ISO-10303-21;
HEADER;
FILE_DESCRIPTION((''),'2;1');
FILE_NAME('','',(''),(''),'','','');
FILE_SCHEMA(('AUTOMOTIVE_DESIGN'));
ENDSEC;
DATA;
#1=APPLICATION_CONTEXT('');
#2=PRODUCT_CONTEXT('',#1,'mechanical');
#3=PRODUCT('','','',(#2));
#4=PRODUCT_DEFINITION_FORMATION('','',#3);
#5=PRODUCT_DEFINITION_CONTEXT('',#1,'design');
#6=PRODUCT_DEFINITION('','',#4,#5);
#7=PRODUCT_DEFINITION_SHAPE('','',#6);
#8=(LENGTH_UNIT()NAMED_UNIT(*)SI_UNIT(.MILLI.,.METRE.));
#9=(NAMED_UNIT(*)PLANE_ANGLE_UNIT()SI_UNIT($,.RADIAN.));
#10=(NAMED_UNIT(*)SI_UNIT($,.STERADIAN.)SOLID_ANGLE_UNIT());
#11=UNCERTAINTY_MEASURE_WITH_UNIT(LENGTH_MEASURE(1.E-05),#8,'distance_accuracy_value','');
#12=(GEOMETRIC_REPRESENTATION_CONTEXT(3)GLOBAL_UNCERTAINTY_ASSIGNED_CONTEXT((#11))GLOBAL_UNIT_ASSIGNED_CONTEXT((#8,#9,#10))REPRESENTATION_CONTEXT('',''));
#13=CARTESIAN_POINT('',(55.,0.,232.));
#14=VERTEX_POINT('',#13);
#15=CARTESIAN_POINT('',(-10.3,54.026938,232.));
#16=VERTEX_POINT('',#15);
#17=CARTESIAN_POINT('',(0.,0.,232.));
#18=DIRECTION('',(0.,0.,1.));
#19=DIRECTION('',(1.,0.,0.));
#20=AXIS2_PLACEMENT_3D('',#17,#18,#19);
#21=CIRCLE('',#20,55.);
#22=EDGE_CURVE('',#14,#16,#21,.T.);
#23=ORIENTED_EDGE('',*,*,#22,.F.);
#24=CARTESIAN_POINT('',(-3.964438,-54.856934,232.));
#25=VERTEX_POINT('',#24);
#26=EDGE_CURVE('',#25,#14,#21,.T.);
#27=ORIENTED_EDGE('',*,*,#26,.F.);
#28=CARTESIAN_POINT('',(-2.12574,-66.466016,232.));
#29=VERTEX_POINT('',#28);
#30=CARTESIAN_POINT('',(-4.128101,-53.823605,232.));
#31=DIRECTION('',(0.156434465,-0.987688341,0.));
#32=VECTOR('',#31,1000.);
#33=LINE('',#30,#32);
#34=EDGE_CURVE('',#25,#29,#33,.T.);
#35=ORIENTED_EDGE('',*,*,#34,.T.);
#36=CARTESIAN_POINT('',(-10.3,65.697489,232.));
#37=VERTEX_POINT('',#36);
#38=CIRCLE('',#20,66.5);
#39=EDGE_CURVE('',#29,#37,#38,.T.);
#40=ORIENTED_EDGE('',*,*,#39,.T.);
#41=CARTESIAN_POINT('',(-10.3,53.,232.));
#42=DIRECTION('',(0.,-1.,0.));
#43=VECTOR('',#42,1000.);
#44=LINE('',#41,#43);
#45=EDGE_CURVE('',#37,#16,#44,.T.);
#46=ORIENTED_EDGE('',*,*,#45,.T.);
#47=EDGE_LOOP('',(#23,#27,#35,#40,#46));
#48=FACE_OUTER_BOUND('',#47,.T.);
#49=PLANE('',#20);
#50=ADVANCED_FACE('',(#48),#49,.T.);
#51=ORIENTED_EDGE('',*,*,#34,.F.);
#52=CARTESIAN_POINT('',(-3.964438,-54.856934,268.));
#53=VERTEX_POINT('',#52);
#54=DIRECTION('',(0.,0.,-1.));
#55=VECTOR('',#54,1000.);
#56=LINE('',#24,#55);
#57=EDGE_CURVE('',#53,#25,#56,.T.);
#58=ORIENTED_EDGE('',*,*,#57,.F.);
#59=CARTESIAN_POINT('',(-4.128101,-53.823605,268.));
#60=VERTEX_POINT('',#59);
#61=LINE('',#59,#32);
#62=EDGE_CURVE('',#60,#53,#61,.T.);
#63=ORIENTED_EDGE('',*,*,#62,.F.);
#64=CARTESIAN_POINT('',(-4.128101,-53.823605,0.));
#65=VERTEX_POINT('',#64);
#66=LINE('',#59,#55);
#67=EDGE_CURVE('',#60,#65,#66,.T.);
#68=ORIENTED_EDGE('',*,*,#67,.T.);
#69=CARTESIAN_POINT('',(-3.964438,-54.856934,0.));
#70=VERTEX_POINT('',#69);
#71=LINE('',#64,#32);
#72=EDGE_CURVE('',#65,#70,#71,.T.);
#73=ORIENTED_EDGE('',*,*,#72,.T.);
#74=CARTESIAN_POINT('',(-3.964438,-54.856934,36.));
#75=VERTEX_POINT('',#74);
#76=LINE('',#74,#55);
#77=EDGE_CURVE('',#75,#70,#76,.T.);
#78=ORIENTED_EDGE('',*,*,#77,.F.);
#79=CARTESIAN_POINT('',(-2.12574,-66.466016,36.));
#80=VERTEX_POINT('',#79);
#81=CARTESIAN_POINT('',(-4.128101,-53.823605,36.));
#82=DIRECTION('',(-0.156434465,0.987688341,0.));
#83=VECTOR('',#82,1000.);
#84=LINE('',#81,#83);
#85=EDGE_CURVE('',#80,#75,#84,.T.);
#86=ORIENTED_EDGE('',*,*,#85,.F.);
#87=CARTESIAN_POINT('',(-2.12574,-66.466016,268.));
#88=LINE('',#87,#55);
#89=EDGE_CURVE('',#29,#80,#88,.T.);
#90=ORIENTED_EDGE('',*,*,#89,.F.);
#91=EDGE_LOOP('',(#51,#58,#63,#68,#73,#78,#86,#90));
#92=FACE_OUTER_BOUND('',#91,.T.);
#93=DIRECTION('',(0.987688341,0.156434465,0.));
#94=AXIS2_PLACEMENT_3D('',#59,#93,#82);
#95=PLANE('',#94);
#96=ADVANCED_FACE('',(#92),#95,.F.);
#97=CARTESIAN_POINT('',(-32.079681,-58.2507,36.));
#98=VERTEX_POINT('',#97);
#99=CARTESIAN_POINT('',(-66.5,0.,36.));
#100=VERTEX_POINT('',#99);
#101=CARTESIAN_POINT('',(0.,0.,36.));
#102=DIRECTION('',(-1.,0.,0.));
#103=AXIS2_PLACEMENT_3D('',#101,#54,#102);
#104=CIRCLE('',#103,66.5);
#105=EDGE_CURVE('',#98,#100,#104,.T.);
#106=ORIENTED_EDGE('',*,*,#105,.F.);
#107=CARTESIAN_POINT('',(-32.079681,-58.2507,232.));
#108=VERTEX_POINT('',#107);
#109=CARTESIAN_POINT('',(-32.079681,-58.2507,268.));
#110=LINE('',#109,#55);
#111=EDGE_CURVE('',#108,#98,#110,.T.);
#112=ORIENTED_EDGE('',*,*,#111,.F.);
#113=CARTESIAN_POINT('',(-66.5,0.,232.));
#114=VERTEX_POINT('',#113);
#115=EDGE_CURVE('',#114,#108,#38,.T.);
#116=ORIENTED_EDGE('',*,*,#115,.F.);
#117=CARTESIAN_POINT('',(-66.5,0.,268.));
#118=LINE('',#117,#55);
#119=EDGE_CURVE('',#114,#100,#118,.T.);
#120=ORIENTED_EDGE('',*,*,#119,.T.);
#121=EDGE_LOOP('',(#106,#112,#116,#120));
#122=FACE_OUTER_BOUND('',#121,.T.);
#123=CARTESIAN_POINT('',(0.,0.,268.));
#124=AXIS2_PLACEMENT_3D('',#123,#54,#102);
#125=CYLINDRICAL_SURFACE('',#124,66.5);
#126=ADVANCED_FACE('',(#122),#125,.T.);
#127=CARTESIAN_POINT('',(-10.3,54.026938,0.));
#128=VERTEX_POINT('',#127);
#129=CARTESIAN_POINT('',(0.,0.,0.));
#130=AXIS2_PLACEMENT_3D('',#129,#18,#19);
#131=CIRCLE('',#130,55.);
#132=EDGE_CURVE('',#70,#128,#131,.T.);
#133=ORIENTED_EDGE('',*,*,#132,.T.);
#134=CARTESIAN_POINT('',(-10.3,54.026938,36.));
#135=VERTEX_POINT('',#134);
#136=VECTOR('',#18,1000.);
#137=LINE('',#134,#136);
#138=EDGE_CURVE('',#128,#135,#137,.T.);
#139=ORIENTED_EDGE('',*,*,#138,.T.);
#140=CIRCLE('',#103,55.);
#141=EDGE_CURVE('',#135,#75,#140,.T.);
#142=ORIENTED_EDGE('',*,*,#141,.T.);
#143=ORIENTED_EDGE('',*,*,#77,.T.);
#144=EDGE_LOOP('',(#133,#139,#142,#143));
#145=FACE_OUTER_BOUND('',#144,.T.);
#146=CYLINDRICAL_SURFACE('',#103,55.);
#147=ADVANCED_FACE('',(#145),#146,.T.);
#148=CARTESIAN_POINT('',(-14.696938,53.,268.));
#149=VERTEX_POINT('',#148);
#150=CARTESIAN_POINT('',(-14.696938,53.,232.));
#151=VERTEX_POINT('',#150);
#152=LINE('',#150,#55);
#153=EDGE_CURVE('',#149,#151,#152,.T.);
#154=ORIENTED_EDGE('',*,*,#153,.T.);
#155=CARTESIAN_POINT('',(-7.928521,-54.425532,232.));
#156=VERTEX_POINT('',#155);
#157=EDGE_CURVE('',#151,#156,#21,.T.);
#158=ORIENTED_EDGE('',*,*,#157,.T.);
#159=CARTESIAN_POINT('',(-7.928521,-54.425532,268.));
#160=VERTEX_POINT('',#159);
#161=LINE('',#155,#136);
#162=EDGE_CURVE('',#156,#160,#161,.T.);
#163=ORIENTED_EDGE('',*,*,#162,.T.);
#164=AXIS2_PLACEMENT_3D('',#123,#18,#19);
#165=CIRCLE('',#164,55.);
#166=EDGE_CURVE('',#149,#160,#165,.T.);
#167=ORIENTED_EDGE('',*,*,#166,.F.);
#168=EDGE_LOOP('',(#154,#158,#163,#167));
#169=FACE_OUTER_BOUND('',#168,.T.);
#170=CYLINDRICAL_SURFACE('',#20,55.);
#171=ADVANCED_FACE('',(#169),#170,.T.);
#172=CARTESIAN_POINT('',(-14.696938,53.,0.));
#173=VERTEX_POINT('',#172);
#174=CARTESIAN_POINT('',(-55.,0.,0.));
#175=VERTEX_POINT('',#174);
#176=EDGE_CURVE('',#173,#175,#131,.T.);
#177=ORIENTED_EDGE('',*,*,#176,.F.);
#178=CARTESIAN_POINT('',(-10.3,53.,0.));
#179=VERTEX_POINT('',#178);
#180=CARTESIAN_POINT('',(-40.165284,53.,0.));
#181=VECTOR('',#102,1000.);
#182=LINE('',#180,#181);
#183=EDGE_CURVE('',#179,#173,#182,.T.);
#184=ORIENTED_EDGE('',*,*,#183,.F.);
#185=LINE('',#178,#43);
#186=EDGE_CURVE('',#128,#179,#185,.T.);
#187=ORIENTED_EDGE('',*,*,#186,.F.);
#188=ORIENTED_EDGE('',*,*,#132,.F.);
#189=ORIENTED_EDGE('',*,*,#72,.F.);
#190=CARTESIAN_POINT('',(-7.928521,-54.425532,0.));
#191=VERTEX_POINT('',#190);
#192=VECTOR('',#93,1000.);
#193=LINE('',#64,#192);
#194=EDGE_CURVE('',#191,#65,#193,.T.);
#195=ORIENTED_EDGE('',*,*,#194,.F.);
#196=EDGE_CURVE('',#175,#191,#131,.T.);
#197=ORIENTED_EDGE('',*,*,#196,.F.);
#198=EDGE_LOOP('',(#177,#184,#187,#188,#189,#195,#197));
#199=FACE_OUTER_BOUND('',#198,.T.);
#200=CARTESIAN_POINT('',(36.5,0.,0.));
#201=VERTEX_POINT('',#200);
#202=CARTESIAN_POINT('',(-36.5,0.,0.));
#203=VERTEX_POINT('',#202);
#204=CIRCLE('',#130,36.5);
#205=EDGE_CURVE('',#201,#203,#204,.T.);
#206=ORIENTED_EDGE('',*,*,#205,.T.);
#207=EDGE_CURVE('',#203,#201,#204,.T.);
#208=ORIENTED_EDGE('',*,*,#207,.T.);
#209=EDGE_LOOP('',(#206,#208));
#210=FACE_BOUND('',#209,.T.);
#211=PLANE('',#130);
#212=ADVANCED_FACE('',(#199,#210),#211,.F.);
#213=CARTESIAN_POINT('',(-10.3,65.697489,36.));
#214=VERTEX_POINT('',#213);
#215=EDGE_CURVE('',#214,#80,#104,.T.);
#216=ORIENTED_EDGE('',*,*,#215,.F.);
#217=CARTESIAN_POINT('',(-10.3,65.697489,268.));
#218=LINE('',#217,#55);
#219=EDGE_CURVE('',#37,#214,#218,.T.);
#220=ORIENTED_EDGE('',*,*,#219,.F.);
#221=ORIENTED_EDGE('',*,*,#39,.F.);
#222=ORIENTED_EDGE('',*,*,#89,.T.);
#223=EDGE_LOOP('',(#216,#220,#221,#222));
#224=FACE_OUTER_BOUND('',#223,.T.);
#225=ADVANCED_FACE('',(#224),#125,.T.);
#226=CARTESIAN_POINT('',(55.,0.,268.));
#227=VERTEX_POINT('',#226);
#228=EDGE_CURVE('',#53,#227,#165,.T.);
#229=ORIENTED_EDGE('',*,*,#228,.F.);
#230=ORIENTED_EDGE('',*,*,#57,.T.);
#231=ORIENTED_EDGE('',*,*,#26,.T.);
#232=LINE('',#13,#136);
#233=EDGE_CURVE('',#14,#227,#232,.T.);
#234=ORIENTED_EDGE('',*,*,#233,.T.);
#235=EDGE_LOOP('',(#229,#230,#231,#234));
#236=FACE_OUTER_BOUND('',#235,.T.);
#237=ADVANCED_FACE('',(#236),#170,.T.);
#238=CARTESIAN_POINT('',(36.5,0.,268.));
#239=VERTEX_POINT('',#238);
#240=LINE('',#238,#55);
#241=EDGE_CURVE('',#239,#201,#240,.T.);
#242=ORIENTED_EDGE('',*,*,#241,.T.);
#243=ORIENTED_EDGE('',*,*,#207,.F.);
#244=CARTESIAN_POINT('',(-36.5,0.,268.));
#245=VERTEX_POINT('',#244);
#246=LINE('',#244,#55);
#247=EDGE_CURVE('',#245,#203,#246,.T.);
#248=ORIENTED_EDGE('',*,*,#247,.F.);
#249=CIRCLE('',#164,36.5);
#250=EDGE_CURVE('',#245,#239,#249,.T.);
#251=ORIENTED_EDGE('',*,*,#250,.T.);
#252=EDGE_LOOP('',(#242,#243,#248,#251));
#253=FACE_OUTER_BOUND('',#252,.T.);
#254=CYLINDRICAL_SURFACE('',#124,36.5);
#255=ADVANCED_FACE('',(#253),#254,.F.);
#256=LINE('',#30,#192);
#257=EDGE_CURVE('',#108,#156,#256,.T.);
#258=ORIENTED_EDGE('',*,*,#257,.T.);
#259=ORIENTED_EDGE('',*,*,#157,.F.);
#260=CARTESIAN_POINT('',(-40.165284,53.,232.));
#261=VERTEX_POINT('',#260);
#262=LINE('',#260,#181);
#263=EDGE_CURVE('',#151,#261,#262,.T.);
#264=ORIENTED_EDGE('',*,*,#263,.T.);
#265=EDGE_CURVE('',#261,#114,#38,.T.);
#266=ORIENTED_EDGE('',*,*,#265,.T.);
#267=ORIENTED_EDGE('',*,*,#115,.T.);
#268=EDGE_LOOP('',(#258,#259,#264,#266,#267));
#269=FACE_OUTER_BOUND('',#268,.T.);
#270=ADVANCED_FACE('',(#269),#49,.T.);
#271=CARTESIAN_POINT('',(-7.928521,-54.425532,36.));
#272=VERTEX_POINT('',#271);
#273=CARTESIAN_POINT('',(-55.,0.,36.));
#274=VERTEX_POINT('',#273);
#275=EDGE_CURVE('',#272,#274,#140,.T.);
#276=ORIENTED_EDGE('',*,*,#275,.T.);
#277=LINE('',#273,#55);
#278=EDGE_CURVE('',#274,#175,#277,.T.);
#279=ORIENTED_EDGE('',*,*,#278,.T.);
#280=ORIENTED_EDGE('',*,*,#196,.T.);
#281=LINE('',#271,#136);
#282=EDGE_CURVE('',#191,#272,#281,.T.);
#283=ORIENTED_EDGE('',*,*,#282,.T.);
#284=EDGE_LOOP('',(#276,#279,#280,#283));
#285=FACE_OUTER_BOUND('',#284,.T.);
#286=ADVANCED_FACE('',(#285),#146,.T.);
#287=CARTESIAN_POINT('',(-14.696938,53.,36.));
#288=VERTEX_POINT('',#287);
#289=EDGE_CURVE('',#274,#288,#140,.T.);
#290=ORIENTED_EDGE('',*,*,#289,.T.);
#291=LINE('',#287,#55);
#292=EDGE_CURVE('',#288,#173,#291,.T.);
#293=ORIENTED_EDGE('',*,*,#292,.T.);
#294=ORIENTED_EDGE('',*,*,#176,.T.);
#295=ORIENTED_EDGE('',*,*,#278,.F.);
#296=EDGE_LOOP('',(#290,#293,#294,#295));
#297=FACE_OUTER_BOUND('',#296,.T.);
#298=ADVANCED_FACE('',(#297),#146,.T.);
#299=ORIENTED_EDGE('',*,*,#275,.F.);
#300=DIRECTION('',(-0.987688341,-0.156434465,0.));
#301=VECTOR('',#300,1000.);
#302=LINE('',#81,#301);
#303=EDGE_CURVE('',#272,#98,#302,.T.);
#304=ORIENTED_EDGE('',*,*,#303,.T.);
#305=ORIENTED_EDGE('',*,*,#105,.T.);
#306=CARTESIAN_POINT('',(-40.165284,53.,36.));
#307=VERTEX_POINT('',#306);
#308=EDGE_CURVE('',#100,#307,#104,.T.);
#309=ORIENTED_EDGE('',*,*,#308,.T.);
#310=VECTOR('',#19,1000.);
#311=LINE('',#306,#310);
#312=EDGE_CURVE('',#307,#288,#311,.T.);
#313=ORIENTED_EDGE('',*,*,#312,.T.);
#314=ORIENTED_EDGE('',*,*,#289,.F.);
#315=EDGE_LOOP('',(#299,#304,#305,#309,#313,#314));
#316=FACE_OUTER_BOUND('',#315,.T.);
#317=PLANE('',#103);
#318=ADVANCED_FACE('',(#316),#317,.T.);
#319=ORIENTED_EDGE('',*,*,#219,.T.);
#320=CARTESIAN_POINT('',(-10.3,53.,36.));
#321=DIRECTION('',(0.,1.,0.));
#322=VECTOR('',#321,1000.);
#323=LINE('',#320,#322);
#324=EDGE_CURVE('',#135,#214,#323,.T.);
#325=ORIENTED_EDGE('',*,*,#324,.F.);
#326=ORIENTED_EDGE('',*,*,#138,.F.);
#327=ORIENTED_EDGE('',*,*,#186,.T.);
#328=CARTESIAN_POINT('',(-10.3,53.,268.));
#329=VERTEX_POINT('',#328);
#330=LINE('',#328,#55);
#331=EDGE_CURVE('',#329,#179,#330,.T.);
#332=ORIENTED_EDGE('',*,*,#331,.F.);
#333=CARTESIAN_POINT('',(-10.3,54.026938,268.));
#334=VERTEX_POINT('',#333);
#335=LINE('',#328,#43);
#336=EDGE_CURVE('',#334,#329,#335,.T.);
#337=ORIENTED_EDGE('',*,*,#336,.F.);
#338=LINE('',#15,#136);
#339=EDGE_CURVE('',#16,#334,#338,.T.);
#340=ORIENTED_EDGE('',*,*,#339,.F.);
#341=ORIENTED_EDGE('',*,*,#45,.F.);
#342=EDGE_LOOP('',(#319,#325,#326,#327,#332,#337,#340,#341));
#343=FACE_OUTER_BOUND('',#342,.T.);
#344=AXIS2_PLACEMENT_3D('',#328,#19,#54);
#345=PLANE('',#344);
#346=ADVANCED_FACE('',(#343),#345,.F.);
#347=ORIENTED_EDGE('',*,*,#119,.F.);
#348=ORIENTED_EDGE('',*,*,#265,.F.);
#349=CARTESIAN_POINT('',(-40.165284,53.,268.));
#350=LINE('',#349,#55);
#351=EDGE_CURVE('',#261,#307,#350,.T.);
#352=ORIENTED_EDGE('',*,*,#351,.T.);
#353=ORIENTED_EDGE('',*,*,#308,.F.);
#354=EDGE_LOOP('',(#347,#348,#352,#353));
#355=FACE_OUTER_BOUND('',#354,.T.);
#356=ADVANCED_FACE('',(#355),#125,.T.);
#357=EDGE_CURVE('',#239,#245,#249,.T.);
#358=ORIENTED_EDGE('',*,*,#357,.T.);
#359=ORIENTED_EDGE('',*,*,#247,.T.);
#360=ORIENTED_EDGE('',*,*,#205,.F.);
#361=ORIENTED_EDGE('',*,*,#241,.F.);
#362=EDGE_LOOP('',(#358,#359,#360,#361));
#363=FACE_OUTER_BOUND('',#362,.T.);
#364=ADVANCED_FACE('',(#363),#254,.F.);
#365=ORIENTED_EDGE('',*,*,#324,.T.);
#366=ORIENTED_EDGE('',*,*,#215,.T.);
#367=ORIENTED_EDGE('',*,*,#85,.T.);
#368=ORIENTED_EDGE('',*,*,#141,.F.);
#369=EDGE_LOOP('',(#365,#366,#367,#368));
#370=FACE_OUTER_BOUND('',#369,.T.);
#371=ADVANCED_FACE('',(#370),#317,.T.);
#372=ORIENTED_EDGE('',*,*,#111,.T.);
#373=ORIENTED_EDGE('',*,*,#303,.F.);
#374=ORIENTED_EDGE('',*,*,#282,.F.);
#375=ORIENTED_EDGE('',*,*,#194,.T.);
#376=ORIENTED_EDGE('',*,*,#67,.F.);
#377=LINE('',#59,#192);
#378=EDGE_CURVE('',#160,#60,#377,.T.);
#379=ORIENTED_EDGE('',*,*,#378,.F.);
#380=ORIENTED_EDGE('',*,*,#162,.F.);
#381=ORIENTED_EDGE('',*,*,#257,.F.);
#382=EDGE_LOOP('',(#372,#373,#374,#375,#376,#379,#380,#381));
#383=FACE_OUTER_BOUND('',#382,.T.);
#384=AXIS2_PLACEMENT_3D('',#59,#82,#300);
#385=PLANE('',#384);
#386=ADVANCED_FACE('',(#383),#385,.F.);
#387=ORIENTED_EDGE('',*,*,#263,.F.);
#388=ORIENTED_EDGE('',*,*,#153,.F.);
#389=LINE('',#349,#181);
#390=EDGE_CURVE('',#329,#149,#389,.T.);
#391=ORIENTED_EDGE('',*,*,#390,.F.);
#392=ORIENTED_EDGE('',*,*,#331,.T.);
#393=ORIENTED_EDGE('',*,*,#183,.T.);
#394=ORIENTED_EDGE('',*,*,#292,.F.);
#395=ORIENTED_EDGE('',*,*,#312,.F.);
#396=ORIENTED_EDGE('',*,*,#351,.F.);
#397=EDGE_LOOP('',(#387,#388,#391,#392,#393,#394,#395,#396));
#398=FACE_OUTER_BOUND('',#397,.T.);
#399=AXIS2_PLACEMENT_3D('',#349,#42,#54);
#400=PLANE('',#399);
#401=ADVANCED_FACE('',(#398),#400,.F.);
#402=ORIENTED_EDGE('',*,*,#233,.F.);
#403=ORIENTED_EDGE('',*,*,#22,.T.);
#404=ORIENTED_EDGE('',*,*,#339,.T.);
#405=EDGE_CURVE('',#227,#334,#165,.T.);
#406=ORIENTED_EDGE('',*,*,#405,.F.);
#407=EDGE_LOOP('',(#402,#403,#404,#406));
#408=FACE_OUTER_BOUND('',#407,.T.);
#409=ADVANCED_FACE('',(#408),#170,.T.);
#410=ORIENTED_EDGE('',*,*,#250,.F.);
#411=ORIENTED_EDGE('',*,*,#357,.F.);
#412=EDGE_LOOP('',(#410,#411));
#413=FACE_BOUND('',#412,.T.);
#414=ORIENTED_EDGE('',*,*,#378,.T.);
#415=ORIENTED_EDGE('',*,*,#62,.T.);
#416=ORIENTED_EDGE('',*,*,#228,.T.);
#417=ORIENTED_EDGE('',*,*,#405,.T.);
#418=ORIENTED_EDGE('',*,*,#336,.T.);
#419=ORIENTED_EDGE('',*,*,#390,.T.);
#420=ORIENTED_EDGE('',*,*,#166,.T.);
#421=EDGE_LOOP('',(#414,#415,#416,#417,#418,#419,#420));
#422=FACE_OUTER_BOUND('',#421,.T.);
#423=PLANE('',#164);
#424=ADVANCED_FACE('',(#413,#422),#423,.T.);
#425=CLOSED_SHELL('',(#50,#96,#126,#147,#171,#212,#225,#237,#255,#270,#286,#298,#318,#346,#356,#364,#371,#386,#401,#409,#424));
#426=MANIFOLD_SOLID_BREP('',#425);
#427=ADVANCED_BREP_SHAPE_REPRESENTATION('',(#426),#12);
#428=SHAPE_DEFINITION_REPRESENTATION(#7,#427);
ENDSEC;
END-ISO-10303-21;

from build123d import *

# Parameters (mm, degrees)
SKETCH1_R           = 36.5
BOSS_EXTRUDE1_DEPTH = 268
SKETCH2_R           = 70
SKETCH2_R_2         = 55
CUT_EXTRUDE1_DEPTH  = 36
CUT_EXTRUDE2_START  = -36
SKETCH3_R           = 70
SKETCH3_R_2         = 55
CUT_EXTRUDE2_DEPTH  = 36


with BuildPart() as part:
    # Sketch1 → Boss-Extrude1 (new body)
    with BuildSketch(Plane.XY):
        with BuildLine():
            Line((-40.165283517, 53), (-10.3, 53))
            Line((-10.3, 53), (-10.3, 65.697488536))
            ThreePointArc((-10.3, 65.697488536), (66.373170096, 4.105154246), (-2.125739686, -66.466015608))
            Line((-2.125739686, -66.466015608), (-4.128100838, -53.823604848))
            Line((-4.128100838, -53.823604848), (-32.079680877, -58.250700209))
            ThreePointArc((-32.079680877, -58.250700209), (-66.325057816, -4.820446627), (-40.165283517, 53))
        make_face()
        Circle(SKETCH1_R, mode=Mode.SUBTRACT)
    extrude(amount=BOSS_EXTRUDE1_DEPTH)

    # Sketch2 → Cut-Extrude1 (cut)
    with BuildSketch(Plane.XY.offset(268)):
        Circle(SKETCH2_R)
        Circle(SKETCH2_R_2, mode=Mode.SUBTRACT)
    extrude(amount=-CUT_EXTRUDE1_DEPTH, mode=Mode.SUBTRACT)

    # Sketch3 → Cut-Extrude2 (cut)
    with BuildSketch(Plane(origin=(0, 0, 0), x_dir=(-1, 0, 0), z_dir=(0, 0, -1)).offset(CUT_EXTRUDE2_START)):
        Circle(SKETCH3_R)
        Circle(SKETCH3_R_2, mode=Mode.SUBTRACT)
    extrude(amount=CUT_EXTRUDE2_DEPTH, mode=Mode.SUBTRACT)


solid = part.part
